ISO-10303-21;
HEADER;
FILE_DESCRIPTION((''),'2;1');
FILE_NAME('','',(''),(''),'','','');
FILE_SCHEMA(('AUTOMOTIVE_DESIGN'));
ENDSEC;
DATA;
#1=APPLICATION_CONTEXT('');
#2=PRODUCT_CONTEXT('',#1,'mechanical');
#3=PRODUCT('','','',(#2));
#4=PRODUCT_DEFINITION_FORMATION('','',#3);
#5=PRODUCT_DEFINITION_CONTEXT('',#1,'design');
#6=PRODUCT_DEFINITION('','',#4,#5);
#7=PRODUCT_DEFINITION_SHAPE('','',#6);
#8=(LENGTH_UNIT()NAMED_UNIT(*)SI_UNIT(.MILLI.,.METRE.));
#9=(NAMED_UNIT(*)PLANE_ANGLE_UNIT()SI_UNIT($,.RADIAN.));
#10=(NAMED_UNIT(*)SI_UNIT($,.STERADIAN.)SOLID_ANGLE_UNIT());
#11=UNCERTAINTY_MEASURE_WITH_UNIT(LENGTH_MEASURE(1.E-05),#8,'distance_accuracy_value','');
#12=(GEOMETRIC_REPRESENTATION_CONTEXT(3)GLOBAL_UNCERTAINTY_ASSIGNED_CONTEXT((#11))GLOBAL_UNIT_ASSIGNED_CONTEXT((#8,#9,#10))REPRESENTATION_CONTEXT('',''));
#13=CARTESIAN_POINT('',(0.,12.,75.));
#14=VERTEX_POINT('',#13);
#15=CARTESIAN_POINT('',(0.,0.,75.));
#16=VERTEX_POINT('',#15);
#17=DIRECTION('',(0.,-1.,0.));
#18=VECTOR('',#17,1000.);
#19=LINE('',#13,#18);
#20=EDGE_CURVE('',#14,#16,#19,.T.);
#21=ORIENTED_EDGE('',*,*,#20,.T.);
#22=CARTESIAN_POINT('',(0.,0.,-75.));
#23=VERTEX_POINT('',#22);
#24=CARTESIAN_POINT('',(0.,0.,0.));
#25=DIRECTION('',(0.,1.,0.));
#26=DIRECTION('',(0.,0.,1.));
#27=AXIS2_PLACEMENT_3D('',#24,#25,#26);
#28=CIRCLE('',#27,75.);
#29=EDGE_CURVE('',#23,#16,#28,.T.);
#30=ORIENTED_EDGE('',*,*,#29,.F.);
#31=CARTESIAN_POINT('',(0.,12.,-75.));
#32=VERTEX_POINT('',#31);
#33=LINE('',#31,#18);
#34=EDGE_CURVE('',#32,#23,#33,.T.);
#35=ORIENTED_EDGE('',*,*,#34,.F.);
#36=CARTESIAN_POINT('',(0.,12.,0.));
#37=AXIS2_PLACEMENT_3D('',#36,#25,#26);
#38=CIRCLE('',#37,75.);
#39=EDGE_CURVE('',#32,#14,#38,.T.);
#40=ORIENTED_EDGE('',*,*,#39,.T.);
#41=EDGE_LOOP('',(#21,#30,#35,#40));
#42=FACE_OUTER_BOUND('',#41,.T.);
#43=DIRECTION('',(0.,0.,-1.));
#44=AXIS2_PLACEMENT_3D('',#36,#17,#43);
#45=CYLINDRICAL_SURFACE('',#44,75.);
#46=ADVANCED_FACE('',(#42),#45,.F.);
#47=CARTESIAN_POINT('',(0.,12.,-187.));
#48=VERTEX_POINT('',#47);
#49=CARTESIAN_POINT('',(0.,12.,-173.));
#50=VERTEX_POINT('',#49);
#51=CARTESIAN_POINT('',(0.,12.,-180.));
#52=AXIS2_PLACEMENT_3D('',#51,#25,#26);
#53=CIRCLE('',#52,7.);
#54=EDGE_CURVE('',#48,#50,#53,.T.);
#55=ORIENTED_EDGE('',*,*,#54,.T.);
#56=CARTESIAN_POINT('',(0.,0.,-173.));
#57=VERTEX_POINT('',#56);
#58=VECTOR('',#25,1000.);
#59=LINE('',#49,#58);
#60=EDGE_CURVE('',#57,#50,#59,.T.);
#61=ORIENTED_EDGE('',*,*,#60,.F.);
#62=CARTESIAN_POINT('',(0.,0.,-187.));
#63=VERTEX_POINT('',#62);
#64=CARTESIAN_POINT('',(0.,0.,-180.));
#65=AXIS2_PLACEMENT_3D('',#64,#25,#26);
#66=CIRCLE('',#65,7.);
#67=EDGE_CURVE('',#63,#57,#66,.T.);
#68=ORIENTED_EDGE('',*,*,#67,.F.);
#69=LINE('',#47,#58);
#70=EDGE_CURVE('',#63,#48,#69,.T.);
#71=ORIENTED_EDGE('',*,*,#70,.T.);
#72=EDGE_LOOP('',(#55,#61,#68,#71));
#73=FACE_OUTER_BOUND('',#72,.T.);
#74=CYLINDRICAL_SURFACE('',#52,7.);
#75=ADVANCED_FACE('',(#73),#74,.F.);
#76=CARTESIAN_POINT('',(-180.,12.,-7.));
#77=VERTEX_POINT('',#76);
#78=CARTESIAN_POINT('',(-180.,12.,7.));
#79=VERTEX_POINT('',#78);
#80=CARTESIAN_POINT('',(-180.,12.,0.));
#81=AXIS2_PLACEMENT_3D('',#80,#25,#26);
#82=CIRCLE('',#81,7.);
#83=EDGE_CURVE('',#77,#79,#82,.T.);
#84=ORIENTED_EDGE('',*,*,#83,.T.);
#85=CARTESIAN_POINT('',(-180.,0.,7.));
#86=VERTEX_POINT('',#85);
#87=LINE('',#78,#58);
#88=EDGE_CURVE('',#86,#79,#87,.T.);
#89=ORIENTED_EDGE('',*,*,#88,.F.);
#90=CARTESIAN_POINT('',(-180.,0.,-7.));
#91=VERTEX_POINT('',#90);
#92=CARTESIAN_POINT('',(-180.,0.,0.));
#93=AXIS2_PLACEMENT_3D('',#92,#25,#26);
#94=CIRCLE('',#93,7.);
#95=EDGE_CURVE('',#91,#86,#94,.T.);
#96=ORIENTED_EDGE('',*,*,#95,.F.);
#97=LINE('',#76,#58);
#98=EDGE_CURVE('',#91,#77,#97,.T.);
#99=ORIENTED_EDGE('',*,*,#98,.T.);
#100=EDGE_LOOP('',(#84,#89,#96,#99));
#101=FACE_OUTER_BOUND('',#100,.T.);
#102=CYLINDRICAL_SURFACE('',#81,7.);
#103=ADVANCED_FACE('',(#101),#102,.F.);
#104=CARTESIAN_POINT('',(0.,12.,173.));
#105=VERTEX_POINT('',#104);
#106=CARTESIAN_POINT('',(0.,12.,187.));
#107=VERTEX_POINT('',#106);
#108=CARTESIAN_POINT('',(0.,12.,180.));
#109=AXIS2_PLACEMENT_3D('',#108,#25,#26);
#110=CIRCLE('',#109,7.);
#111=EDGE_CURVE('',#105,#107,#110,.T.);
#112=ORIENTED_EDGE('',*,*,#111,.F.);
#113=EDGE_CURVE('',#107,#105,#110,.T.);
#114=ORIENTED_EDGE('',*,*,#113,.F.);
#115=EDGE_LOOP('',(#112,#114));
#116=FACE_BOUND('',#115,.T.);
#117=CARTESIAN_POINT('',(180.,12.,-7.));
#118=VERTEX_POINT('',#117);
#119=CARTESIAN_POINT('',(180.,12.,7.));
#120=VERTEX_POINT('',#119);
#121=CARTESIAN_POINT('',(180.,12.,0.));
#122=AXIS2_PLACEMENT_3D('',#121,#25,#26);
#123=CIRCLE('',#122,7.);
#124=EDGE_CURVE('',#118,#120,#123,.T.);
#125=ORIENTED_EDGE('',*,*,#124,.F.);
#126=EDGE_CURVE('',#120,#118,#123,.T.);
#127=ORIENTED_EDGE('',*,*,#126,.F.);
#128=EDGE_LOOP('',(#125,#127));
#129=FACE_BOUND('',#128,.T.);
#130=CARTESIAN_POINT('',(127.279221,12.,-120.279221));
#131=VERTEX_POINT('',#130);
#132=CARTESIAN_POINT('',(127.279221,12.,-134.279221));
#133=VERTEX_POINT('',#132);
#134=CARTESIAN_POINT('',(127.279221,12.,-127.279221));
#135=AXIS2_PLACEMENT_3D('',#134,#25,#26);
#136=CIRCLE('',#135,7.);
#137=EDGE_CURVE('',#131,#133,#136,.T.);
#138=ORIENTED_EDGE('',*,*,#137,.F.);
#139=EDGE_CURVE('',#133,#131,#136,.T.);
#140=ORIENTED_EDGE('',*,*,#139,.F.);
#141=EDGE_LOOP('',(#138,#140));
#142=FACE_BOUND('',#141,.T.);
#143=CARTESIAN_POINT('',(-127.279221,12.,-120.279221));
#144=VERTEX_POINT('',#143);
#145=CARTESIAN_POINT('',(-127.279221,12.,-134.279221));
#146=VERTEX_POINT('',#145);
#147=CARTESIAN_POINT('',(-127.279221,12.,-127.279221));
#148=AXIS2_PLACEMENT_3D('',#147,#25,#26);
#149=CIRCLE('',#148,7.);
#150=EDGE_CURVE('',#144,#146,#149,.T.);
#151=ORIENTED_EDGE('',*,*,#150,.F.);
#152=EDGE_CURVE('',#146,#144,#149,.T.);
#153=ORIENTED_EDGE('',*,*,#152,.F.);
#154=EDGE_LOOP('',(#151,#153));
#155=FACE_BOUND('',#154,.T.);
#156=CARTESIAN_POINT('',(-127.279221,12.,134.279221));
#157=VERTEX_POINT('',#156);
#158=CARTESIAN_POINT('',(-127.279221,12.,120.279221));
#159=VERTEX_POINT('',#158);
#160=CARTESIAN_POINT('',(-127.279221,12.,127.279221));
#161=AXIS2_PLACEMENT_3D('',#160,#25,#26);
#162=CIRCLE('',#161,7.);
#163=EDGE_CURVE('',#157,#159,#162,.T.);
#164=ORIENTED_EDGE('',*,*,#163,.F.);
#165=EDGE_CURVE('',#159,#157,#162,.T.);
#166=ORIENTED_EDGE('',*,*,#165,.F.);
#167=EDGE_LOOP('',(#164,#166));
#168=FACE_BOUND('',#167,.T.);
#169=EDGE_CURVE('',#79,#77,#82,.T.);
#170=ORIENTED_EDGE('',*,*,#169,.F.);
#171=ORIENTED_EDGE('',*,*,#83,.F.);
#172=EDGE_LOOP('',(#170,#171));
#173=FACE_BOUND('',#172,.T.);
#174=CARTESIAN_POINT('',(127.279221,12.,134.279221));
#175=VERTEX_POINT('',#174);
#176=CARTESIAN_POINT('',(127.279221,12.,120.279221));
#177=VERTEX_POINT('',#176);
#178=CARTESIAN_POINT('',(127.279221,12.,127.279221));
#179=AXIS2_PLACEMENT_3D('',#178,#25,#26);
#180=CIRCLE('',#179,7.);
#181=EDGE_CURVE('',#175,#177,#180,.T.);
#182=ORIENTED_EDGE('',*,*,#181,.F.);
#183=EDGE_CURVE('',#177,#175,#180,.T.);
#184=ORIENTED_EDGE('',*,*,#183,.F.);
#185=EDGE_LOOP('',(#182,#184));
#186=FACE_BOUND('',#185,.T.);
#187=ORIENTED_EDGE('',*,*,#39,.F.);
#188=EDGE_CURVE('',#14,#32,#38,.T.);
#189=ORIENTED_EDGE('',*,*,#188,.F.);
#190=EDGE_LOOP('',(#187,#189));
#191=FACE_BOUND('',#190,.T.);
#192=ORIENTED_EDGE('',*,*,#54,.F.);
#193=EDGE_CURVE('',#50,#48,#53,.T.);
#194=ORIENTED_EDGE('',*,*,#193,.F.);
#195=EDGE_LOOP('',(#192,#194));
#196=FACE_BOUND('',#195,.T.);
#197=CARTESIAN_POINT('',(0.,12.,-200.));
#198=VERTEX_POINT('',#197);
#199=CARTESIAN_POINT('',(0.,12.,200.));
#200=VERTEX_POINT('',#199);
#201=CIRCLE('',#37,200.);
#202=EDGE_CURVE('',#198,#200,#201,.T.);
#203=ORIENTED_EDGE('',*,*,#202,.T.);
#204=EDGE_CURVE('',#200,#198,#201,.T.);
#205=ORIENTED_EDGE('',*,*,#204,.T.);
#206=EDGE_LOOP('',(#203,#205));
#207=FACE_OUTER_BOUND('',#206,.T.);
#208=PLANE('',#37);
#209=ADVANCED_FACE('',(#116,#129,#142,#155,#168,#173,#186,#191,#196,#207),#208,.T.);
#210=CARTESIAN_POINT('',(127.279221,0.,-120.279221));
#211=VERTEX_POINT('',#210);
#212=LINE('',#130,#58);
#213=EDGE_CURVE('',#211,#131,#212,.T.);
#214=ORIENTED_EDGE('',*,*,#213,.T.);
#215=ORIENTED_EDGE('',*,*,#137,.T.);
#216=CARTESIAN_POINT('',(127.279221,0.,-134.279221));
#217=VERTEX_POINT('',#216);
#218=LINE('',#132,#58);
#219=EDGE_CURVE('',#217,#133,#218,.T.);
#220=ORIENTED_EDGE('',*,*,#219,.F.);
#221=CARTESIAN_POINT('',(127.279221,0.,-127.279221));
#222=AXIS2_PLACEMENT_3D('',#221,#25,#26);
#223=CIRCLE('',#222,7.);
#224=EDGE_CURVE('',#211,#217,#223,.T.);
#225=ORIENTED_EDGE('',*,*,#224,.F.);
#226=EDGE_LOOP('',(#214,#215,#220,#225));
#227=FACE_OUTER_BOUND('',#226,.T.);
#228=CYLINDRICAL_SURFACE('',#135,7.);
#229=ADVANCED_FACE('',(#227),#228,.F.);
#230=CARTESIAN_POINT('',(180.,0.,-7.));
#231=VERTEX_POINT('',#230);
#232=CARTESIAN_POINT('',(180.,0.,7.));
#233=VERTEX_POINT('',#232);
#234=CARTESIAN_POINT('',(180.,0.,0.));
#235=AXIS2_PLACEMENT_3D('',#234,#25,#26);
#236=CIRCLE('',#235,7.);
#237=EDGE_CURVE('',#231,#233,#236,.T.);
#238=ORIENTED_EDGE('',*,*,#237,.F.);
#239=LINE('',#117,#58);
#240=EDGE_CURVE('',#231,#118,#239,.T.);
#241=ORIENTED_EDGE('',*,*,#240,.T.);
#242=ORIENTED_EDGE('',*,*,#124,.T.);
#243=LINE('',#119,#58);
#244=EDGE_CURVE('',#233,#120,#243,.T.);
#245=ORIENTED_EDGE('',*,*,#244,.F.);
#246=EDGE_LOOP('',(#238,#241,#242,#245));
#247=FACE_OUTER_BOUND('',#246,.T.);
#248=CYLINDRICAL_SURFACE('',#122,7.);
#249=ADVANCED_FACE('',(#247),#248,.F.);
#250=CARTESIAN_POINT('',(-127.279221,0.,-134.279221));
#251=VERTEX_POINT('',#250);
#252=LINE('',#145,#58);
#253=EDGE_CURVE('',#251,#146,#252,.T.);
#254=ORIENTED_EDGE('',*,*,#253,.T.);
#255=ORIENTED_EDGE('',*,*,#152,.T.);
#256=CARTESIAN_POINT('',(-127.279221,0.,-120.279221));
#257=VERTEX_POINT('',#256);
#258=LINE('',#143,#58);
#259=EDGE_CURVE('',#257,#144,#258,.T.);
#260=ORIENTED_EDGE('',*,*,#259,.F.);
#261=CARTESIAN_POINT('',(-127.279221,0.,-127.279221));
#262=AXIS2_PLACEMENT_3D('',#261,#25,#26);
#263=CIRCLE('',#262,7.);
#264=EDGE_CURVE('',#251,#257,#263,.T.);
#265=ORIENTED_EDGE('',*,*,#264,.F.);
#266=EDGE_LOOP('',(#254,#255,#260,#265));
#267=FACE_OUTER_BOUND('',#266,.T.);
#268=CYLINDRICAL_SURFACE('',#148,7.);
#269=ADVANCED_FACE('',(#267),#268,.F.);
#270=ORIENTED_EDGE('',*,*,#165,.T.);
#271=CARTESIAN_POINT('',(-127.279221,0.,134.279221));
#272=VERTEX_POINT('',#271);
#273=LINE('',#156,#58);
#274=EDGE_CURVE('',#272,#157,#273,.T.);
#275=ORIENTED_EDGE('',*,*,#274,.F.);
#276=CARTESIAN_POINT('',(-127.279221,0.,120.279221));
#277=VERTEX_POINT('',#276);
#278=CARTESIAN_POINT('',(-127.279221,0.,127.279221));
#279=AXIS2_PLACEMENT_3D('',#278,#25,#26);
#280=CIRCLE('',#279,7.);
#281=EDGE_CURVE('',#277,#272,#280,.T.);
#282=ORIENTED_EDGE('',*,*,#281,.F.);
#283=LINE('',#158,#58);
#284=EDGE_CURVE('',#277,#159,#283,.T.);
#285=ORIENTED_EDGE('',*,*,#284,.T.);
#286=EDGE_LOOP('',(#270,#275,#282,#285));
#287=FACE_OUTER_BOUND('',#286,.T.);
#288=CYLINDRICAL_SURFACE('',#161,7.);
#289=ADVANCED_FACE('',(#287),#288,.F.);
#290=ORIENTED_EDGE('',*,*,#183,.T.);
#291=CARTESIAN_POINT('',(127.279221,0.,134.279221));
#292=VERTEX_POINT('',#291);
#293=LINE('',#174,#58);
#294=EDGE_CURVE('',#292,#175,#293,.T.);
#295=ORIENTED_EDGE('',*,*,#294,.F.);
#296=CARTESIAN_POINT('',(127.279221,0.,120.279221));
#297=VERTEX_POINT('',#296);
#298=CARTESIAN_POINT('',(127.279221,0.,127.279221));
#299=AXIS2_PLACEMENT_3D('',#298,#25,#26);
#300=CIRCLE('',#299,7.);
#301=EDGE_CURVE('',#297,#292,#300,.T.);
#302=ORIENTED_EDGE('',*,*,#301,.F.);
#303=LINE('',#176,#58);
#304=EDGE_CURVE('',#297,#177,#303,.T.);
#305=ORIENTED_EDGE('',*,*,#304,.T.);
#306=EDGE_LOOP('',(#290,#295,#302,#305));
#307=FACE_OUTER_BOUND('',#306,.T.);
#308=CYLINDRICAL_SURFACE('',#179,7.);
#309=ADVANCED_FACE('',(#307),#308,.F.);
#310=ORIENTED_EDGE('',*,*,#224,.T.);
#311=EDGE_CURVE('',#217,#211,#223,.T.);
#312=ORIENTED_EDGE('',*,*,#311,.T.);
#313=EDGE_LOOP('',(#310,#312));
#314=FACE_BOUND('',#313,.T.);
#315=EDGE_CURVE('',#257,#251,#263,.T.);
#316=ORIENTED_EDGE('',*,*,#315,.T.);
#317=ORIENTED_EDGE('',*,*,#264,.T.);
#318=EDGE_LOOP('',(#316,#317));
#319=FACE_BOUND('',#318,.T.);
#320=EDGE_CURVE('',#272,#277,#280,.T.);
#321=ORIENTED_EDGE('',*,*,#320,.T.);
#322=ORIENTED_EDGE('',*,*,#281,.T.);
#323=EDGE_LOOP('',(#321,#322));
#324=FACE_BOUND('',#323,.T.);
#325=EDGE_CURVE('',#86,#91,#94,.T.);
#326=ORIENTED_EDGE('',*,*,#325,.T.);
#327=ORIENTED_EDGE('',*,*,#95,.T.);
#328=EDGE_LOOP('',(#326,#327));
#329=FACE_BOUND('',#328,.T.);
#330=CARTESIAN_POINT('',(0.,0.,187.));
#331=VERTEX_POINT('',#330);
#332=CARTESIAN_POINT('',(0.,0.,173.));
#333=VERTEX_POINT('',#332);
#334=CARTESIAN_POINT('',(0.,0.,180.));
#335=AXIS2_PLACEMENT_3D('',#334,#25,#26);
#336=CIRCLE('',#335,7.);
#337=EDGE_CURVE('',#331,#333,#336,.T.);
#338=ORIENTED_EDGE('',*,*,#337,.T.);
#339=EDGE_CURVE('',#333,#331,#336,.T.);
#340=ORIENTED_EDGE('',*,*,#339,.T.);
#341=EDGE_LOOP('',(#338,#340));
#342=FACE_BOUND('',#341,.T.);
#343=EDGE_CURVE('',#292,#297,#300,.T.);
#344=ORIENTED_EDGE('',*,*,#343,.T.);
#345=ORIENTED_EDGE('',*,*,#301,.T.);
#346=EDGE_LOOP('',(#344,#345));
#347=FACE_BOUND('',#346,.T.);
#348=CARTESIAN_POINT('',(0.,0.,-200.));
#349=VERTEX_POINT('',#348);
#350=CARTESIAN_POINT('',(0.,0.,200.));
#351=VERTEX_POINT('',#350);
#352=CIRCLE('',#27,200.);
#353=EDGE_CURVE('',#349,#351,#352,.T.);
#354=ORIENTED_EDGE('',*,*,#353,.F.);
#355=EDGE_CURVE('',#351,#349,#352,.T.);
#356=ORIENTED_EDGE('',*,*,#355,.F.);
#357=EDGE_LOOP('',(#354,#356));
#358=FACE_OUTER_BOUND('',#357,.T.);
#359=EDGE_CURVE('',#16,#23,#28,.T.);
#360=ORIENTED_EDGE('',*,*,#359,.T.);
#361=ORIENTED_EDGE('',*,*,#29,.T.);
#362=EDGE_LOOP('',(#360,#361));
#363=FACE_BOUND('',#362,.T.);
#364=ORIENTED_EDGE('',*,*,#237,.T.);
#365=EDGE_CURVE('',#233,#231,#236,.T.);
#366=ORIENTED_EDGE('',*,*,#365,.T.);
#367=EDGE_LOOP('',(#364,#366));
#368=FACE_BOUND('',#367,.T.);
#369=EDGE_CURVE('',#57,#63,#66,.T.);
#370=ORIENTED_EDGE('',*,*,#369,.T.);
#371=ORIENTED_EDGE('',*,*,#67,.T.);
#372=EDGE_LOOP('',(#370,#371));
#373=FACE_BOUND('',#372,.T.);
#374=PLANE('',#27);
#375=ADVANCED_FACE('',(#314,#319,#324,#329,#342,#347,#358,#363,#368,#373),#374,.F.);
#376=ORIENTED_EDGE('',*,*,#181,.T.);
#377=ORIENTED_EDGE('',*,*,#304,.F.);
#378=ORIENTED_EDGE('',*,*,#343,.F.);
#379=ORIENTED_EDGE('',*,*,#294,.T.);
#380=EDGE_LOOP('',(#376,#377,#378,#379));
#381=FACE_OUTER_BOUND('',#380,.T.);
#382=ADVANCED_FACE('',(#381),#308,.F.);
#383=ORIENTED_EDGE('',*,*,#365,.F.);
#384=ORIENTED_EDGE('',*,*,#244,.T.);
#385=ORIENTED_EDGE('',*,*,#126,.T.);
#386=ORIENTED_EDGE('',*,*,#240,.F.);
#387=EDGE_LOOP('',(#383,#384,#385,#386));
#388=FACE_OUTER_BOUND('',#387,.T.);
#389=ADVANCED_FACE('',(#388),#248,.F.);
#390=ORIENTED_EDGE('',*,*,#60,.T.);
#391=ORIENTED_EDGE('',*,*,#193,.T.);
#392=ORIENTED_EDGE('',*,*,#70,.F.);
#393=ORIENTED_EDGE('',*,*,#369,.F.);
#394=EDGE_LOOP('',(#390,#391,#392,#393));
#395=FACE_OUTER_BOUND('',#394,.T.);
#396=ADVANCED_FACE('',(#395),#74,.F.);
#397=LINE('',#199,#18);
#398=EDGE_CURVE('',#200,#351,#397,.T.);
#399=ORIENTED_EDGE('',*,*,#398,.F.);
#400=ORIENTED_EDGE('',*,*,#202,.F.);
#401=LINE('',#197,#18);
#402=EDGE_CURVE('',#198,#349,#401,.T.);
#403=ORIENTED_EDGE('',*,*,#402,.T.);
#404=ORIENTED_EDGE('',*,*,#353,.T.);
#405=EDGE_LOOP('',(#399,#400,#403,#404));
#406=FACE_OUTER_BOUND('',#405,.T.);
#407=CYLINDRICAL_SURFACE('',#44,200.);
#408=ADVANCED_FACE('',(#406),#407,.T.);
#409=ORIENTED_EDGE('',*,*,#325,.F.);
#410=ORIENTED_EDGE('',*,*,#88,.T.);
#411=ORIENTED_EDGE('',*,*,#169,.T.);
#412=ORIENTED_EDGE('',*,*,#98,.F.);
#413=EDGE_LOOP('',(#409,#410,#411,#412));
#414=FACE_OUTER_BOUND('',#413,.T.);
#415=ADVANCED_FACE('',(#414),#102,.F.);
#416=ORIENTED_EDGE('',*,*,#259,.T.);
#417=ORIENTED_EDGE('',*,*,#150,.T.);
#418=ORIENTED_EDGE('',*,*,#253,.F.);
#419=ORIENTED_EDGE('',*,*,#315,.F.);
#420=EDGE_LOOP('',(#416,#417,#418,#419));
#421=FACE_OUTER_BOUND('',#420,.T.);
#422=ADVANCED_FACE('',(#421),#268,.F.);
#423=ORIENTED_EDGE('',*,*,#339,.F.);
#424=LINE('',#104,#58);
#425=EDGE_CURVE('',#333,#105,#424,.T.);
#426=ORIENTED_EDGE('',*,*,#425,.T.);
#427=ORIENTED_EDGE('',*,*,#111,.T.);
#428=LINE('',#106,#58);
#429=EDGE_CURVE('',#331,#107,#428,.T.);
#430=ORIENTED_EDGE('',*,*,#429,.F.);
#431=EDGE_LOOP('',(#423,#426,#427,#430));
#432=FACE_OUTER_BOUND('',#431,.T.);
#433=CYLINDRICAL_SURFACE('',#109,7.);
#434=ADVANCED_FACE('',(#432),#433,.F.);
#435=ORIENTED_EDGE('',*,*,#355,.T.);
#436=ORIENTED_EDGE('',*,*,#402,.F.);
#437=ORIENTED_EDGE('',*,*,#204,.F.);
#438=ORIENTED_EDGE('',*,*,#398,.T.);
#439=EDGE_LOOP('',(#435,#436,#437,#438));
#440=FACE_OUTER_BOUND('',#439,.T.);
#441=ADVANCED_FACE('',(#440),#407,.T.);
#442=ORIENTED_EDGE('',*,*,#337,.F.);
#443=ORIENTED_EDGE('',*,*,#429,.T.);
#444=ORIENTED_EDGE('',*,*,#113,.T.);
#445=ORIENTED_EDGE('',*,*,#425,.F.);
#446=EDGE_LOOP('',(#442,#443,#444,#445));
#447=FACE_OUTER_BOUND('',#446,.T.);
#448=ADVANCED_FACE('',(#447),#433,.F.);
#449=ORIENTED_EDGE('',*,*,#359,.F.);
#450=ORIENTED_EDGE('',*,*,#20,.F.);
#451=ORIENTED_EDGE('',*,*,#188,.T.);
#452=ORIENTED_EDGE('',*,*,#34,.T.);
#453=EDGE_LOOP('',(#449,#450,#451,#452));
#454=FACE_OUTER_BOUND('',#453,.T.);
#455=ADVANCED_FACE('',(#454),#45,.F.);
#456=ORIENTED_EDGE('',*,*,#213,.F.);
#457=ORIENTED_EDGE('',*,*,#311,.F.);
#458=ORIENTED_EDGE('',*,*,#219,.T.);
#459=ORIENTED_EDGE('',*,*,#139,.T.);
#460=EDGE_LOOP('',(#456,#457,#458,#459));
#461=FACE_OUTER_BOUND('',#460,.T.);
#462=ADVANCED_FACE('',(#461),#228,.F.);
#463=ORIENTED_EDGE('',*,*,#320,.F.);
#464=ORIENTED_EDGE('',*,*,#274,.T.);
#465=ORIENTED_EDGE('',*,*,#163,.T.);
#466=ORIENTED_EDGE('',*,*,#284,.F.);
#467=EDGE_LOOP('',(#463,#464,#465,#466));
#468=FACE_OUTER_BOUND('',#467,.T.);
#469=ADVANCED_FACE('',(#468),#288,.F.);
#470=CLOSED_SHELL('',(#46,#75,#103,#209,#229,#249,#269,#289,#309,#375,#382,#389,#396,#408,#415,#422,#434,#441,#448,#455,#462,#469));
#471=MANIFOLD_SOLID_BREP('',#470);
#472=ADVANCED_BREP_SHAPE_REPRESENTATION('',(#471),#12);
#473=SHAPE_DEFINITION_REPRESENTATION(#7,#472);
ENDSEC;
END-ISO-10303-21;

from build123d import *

# Parameters (mm, degrees)
SKETCH1_R                  = 200
SKETCH1_R_2                = 75
BOSS_EXTRUDE1_DEPTH        = 12
F_14_0_14_DIAMETER_HOLE1_D = 14


with BuildPart() as part:
    # Sketch1 → Boss-Extrude1 (new body)
    with BuildSketch(Plane(origin=(0, 0, 0), x_dir=(1, 0, 0), z_dir=(0, 1, 0))):
        with Locations(Location((0, 0, 0), (0, 0, 270))):
            Circle(SKETCH1_R)
        with Locations(Location((0, 0, 0), (0, 0, 270))):
            Circle(SKETCH1_R_2, mode=Mode.SUBTRACT)
    extrude(amount=BOSS_EXTRUDE1_DEPTH)

    # Ø14.0 (14) Diameter Hole1 (through all)
    with Locations(Plane(origin=(0, 12, 0), x_dir=(1, 0, 0), z_dir=(0, 1, 0))):
        with Locations((0, 180), (127.279220614, 127.279220614), (180, 0), (127.279220614, -127.279220614), (0, -180), (-127.279220614, -127.279220614), (-180, 0), (-127.279220614, 127.279220614)):
            Hole(F_14_0_14_DIAMETER_HOLE1_D / 2)


solid = part.part
